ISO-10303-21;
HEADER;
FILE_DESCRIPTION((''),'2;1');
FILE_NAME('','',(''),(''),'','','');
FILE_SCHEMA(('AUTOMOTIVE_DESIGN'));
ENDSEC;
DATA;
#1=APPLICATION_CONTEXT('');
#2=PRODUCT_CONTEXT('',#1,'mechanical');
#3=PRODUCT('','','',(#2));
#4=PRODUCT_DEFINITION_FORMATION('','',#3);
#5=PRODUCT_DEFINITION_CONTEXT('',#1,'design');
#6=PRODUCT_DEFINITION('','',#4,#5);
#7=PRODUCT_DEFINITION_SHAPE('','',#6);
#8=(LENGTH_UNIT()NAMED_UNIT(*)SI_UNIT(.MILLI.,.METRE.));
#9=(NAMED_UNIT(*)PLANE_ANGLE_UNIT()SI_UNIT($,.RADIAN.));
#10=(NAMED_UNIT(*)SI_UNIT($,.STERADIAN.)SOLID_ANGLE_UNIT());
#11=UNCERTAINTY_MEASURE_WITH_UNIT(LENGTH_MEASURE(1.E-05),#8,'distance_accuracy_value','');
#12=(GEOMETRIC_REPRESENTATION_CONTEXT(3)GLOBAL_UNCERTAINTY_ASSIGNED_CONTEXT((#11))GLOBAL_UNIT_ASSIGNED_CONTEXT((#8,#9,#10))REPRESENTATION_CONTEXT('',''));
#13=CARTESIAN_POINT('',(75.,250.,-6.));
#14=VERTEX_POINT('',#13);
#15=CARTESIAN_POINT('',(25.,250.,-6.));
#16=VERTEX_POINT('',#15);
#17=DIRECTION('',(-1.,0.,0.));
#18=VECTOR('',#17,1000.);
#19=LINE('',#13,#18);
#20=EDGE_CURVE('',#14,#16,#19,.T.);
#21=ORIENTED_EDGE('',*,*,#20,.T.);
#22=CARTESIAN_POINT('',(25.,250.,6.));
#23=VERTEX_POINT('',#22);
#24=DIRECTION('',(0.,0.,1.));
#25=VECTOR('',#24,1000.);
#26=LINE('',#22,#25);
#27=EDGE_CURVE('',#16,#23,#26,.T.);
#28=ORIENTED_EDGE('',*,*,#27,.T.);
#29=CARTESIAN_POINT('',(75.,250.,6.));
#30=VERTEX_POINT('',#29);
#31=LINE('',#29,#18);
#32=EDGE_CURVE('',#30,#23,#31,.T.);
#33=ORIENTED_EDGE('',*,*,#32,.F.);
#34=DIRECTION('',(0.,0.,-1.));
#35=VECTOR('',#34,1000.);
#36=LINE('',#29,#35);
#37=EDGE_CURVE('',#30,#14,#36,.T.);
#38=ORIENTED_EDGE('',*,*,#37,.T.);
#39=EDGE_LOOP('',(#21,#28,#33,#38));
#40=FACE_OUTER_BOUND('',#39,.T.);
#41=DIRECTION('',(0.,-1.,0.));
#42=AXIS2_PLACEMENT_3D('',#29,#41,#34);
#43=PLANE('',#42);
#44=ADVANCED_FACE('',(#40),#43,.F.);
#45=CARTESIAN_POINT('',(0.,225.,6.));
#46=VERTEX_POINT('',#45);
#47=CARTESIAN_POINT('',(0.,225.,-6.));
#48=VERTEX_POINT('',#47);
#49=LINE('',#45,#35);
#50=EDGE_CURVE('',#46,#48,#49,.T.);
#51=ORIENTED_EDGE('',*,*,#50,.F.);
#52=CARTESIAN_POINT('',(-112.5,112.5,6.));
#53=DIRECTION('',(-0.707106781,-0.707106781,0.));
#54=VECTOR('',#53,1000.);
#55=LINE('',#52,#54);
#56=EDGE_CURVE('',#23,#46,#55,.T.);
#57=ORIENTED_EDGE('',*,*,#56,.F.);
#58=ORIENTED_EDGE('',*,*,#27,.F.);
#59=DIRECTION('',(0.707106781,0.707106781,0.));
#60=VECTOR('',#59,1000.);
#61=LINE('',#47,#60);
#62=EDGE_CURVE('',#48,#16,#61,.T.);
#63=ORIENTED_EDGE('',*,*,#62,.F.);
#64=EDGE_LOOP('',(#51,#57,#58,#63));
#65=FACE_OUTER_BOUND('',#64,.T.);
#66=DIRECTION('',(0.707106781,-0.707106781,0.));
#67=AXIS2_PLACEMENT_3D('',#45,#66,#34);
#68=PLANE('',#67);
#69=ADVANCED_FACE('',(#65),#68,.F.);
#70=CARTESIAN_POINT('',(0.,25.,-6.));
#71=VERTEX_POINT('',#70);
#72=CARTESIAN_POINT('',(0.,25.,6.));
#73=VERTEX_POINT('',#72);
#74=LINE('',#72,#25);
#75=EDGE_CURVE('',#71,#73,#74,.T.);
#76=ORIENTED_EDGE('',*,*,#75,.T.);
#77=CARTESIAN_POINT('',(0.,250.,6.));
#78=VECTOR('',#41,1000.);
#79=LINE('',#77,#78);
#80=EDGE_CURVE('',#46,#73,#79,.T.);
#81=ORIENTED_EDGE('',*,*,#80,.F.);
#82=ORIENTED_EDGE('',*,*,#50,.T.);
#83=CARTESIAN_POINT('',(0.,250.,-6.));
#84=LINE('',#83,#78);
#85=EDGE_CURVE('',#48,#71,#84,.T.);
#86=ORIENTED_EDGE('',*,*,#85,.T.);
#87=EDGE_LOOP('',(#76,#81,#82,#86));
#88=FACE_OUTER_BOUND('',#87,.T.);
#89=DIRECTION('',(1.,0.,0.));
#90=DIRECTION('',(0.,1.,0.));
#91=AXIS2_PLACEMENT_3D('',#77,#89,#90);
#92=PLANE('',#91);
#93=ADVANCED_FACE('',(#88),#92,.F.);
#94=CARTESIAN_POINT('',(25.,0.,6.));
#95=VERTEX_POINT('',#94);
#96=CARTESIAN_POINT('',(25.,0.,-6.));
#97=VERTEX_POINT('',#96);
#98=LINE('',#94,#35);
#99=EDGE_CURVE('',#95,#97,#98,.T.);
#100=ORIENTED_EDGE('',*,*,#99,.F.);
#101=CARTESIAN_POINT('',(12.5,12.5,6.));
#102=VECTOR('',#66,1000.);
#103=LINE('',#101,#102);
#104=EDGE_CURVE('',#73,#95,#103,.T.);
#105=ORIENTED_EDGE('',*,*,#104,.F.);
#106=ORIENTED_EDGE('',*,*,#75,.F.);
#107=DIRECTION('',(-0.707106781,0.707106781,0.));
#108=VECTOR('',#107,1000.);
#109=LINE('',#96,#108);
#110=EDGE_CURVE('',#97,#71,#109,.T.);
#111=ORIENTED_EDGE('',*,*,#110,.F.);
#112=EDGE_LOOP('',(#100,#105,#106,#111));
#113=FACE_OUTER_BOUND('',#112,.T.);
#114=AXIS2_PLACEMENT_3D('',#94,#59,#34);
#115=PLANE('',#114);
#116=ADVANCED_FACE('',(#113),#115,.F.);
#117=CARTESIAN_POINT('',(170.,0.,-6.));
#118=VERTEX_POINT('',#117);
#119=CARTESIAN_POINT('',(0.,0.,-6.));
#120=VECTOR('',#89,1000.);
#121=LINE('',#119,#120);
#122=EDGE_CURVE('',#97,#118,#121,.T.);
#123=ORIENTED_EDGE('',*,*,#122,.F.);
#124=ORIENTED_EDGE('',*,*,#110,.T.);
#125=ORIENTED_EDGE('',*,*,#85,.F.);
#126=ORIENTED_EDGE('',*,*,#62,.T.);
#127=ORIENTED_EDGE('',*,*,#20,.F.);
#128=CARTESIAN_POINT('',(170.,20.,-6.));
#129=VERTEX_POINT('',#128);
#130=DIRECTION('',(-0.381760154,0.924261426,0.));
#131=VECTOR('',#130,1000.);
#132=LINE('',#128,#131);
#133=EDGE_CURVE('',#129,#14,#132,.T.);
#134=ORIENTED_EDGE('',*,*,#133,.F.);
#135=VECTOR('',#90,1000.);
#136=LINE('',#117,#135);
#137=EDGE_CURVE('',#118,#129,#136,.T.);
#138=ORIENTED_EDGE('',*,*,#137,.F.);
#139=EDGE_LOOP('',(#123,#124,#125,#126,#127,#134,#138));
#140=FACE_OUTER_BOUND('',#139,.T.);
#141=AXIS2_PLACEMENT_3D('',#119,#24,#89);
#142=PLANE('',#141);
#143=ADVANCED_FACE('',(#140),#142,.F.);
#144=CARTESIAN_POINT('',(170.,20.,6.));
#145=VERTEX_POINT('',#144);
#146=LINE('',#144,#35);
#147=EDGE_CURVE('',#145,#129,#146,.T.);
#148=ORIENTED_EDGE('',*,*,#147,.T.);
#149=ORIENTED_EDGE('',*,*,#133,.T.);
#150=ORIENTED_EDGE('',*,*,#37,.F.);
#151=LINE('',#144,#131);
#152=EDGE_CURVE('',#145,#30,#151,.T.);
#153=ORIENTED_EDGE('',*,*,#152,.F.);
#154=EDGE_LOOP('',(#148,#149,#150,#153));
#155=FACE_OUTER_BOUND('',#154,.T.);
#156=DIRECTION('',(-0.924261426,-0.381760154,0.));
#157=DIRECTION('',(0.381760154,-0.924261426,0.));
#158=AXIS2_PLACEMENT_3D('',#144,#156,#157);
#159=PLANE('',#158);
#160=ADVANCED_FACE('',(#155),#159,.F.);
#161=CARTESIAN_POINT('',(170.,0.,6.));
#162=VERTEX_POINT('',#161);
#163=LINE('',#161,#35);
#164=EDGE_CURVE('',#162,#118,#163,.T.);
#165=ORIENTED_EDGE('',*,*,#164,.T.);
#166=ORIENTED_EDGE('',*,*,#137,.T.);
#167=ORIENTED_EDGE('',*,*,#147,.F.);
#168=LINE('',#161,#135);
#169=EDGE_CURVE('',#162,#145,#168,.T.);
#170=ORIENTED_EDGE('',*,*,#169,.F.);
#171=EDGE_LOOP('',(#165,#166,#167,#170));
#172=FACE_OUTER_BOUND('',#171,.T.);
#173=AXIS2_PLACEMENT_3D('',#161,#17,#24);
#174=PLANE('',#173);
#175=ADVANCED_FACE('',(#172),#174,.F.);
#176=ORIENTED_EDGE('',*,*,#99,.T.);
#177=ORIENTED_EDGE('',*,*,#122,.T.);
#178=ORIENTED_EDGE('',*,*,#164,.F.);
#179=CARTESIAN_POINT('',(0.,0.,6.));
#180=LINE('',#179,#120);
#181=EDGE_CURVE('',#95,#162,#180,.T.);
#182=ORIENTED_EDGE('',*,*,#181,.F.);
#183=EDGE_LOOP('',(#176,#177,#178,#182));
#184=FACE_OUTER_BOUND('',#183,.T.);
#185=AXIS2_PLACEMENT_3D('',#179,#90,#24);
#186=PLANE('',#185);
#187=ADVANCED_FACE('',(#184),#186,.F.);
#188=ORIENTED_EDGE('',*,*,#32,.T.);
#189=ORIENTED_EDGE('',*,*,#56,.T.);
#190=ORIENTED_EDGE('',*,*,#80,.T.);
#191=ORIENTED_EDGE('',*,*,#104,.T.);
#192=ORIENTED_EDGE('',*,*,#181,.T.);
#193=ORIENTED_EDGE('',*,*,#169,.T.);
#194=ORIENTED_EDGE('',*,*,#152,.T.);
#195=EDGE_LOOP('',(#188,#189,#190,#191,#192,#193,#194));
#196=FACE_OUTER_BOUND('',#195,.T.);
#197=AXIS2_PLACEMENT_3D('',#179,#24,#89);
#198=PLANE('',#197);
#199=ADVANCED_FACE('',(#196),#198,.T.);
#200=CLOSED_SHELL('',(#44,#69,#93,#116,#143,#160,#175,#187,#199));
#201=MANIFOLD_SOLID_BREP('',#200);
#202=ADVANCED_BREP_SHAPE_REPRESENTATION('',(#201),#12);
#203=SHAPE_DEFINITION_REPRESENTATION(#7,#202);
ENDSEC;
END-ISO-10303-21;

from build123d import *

# Parameters (mm, degrees)
BOSS_EXTRUDE1_DEPTH = 6
CHAMFER1_SIZE       = 25


with BuildPart() as part:
    # Sketch1 → Boss-Extrude1 (new, symmetric)
    with BuildSketch(Plane.XY):
        Polygon((0, 0), (170, 0), (170, 20), (75, 250), (0, 250), align=None)
    extrude(amount=BOSS_EXTRUDE1_DEPTH, both=True)

    # Chamfer1
    chamfer1_edges = [part.edges().sort_by_distance(p)[0] for p in [
        (0, 250, 0),
        (0, 0, 0),
    ]]
    chamfer(chamfer1_edges, length=CHAMFER1_SIZE)


solid = part.part
